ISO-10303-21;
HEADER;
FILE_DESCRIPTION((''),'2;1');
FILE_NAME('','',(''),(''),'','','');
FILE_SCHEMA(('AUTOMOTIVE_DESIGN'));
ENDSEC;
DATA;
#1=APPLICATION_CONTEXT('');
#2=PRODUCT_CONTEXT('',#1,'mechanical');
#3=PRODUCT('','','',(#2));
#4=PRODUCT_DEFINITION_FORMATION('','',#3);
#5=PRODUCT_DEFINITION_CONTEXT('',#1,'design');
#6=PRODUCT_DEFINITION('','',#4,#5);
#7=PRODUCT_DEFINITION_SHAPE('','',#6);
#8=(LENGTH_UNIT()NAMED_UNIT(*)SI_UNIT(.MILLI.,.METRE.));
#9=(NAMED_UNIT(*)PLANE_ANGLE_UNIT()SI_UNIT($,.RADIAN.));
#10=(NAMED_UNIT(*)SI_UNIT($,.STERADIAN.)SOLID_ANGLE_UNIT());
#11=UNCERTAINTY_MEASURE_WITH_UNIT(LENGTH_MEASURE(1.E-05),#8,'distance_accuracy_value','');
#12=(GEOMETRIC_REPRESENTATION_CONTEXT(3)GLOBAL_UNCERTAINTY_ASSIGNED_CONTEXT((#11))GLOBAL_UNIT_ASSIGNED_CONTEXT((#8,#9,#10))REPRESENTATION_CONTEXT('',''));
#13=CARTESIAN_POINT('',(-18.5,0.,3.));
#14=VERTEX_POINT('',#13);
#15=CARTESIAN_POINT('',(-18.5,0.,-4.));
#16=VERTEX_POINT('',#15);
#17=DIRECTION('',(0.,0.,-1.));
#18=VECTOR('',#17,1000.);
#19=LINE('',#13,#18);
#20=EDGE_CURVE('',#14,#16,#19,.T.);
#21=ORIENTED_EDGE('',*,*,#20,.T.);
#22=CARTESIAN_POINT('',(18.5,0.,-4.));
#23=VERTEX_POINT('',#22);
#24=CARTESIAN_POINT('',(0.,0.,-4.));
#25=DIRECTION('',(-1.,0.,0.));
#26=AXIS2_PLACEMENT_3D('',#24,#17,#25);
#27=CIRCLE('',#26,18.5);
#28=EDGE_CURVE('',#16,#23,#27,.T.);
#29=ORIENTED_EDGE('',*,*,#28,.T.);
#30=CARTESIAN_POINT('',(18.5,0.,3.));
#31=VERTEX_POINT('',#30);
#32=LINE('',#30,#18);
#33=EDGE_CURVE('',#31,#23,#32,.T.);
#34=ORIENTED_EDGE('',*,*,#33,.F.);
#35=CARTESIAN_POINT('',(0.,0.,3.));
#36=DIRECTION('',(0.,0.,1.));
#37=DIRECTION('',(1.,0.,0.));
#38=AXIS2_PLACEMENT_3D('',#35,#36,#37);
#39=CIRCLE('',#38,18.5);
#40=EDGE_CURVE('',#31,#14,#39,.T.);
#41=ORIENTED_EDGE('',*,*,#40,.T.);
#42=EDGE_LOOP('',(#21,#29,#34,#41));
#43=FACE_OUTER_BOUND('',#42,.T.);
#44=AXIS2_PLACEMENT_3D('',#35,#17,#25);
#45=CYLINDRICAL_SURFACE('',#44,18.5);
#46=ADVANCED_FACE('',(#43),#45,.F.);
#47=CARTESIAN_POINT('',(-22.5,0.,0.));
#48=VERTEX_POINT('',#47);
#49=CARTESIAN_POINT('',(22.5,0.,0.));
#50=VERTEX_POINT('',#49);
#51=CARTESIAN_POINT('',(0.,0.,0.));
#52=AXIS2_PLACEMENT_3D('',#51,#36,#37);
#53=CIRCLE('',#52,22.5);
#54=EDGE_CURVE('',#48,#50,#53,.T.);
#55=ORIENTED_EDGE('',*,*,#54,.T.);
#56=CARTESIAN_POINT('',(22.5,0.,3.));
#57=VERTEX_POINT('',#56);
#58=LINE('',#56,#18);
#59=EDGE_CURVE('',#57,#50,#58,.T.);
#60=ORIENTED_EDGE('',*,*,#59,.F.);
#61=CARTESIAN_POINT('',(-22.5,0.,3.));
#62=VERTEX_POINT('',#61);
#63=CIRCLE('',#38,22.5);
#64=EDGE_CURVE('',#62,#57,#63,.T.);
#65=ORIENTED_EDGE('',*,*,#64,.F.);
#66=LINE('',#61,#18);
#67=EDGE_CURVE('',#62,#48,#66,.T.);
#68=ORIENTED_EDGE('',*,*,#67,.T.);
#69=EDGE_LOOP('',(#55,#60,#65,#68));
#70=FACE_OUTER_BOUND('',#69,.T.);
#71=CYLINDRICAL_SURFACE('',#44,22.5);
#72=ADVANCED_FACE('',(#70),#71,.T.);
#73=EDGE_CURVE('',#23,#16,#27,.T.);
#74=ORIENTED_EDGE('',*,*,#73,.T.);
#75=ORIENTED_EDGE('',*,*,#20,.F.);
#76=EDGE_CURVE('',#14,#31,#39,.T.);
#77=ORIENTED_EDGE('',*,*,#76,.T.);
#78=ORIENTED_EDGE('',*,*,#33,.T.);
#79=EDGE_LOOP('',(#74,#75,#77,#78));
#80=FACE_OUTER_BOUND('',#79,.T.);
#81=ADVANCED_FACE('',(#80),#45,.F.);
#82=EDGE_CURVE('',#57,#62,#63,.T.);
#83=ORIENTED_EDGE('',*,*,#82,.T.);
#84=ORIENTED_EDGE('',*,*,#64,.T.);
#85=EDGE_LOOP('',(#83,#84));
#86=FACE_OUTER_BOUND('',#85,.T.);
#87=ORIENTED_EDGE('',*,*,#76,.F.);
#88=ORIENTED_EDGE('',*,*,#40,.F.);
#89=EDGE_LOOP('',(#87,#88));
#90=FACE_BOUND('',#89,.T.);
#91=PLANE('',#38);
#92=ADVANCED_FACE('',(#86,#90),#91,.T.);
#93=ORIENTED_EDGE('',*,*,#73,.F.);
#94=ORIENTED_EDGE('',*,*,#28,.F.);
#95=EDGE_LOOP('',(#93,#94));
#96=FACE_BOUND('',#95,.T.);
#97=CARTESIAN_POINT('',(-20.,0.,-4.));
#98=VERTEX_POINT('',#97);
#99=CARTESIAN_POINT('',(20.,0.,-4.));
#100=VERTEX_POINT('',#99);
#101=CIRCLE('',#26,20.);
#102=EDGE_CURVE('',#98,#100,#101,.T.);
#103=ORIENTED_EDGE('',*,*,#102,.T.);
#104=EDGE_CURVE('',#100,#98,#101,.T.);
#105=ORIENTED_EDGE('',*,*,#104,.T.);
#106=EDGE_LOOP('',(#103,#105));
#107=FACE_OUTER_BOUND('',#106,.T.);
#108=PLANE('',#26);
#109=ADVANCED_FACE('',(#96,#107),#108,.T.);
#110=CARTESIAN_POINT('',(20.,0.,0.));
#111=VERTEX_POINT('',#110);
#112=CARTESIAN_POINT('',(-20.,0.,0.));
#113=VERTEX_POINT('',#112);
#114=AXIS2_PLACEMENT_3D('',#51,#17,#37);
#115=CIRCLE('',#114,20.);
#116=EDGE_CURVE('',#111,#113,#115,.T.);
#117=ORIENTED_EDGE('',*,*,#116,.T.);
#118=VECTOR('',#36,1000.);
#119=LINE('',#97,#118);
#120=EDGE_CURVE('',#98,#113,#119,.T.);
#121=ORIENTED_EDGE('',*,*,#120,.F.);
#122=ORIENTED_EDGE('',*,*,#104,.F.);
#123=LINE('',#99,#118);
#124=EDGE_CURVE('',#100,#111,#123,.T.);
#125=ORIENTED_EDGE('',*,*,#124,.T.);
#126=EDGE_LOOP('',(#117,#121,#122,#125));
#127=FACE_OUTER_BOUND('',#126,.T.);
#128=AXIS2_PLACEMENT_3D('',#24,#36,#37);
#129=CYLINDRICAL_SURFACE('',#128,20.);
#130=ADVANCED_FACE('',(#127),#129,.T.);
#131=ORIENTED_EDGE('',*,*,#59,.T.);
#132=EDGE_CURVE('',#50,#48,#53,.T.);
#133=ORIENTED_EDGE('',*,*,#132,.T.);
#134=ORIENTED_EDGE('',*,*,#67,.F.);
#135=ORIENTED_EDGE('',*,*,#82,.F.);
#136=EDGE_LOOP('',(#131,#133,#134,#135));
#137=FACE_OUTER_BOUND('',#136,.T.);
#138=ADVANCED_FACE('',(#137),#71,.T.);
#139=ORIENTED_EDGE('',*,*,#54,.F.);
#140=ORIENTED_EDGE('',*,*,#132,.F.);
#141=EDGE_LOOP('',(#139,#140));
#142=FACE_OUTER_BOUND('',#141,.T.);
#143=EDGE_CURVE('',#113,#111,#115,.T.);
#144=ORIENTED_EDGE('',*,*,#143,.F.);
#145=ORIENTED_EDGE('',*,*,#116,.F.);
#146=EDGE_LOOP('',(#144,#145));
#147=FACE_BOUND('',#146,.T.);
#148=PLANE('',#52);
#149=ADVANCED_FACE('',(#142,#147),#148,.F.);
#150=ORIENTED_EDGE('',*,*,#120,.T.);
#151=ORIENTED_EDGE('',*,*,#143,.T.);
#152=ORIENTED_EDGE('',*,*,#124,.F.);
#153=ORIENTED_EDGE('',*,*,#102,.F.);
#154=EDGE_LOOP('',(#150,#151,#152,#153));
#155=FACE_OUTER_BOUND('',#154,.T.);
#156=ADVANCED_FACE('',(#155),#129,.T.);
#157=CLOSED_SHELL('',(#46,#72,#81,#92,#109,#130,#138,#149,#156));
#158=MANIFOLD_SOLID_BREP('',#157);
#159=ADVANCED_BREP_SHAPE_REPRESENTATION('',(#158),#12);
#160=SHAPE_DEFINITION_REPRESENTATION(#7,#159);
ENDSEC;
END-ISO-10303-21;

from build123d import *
from build123d.topology import SkipClean

# Parameters (mm, degrees)
SKETCH1_R           = 22.5
SKETCH1_R_2         = 18.5
BOSS_EXTRUDE1_DEPTH = 3
BOSS_EXTRUDE2_START = 4
SKETCH3_R           = 20
SKETCH3_R_2         = 18.5
BOSS_EXTRUDE2_DEPTH = 4


with BuildPart() as part:
    # Sketch1 → Boss-Extrude1 (new body)
    with BuildSketch(Plane.XY):
        Circle(SKETCH1_R)
        Circle(SKETCH1_R_2, mode=Mode.SUBTRACT)
    extrude(amount=BOSS_EXTRUDE1_DEPTH)

    # Sketch3 → Boss-Extrude2 (add)
    with SkipClean():  # the faces are left unmerged after this step: merging them gives an invalid solid
        with BuildSketch(Plane(origin=(0, 0, 0), x_dir=(-1, 0, 0), z_dir=(0, 0, -1)).offset(BOSS_EXTRUDE2_START)):
            with Locations(Location((0, 0, 0), (0, 0, 180))):
                Circle(SKETCH3_R)
            Circle(SKETCH3_R_2, mode=Mode.SUBTRACT)
        extrude(amount=-BOSS_EXTRUDE2_DEPTH)


solid = part.part
